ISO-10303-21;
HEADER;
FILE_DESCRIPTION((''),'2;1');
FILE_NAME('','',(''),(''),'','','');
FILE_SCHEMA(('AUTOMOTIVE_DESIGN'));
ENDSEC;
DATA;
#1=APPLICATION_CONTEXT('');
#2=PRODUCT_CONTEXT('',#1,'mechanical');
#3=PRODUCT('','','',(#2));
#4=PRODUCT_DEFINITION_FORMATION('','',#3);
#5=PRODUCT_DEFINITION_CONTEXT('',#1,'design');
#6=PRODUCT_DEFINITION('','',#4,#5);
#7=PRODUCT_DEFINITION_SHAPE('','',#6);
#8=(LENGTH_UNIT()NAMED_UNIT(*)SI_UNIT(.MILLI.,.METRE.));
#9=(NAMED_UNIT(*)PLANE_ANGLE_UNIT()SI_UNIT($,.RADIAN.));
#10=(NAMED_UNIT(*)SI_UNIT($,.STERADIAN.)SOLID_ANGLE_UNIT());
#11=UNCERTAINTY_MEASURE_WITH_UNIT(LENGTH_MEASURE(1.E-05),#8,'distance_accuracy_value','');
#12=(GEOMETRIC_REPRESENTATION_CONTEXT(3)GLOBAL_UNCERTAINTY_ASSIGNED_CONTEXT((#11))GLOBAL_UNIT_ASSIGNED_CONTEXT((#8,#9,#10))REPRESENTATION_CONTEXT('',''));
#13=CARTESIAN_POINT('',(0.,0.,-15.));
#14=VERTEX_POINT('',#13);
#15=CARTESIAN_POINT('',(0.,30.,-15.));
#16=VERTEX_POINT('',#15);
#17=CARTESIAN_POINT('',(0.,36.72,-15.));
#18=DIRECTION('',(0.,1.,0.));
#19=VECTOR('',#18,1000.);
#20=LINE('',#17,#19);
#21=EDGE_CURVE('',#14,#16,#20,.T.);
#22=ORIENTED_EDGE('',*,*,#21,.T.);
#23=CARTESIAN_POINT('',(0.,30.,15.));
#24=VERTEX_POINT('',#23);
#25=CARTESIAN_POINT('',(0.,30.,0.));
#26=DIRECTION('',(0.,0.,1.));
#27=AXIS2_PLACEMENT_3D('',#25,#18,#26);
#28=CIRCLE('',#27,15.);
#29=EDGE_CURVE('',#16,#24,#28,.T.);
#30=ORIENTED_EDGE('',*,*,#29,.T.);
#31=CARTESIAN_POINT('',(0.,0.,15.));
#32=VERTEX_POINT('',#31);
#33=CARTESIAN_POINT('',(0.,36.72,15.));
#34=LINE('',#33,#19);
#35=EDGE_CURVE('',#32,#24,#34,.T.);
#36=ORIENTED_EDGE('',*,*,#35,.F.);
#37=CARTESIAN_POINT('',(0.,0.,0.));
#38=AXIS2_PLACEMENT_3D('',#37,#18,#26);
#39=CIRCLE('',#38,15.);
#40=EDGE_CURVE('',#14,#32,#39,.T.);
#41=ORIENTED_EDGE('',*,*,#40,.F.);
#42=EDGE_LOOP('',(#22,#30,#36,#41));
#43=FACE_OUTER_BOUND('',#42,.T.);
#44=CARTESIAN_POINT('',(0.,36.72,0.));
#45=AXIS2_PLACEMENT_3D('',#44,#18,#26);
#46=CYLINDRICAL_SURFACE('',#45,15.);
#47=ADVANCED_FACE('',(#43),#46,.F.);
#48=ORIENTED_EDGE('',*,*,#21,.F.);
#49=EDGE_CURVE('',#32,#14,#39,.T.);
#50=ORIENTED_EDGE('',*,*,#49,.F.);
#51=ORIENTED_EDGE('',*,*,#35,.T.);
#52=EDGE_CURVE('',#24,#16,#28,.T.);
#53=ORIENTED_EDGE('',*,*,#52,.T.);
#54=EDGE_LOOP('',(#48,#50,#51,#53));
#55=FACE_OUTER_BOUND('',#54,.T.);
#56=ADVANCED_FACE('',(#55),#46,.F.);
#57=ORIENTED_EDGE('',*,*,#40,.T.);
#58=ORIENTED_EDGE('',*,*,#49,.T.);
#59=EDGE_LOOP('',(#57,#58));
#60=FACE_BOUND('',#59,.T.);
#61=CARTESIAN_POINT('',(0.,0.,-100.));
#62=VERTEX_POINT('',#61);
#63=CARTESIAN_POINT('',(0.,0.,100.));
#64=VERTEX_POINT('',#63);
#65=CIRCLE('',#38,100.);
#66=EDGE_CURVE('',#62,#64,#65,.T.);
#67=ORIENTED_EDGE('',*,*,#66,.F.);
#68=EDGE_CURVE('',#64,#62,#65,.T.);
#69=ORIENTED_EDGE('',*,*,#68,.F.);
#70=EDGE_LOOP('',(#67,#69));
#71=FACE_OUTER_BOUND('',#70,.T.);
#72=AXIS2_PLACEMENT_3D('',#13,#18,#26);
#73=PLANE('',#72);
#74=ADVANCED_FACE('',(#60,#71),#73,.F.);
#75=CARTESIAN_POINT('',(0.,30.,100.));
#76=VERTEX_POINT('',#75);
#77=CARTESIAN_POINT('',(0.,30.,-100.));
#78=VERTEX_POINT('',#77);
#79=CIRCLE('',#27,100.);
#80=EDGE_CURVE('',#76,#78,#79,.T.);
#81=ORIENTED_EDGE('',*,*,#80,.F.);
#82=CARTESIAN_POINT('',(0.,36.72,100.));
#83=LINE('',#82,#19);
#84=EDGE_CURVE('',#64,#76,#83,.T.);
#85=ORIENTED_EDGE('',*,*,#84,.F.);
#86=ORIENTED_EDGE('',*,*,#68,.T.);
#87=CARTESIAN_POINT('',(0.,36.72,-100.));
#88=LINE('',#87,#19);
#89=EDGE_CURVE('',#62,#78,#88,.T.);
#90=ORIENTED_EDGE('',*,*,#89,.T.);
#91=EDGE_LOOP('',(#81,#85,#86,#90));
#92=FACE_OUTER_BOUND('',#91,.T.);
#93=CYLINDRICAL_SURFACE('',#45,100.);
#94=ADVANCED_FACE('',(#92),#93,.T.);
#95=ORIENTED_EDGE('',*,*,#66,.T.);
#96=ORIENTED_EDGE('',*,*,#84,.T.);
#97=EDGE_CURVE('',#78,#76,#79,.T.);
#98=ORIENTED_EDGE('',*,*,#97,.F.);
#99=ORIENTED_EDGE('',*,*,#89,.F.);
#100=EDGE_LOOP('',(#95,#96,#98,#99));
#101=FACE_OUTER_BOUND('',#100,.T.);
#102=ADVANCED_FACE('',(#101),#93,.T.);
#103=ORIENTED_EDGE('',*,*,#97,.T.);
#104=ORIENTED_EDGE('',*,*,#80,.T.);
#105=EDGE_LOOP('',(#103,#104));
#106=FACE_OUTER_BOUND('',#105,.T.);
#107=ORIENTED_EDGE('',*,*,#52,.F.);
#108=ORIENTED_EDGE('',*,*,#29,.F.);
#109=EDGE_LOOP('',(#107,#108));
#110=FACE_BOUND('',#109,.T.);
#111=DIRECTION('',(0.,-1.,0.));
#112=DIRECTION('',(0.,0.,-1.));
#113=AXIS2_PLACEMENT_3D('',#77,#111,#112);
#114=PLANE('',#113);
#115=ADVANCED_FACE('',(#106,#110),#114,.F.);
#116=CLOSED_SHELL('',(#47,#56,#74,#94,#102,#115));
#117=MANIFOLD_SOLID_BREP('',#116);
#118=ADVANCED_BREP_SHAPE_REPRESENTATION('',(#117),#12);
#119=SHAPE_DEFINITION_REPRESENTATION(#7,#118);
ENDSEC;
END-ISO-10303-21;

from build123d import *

# Parameters (mm, degrees)
SKETCH_1_W = 85
SKETCH_1_H = 30


with BuildPart() as part:
    # 草图1 → 旋转2 (revolve)
    with BuildSketch(Plane(origin=(0, 0, 0), x_dir=(0, 0, -1), z_dir=(1, 0, 0)), mode=Mode.PRIVATE) as revolve_2_sk:
        with Locations((57.5, 15)):
            Rectangle(SKETCH_1_W, SKETCH_1_H)
    revolve(revolve_2_sk.sketch.rotate(Axis((0, 36.72, 0), (0, -1, 0)), 180), axis=Axis((0, 36.72, 0), (0, -1, 0)))


solid = part.part
